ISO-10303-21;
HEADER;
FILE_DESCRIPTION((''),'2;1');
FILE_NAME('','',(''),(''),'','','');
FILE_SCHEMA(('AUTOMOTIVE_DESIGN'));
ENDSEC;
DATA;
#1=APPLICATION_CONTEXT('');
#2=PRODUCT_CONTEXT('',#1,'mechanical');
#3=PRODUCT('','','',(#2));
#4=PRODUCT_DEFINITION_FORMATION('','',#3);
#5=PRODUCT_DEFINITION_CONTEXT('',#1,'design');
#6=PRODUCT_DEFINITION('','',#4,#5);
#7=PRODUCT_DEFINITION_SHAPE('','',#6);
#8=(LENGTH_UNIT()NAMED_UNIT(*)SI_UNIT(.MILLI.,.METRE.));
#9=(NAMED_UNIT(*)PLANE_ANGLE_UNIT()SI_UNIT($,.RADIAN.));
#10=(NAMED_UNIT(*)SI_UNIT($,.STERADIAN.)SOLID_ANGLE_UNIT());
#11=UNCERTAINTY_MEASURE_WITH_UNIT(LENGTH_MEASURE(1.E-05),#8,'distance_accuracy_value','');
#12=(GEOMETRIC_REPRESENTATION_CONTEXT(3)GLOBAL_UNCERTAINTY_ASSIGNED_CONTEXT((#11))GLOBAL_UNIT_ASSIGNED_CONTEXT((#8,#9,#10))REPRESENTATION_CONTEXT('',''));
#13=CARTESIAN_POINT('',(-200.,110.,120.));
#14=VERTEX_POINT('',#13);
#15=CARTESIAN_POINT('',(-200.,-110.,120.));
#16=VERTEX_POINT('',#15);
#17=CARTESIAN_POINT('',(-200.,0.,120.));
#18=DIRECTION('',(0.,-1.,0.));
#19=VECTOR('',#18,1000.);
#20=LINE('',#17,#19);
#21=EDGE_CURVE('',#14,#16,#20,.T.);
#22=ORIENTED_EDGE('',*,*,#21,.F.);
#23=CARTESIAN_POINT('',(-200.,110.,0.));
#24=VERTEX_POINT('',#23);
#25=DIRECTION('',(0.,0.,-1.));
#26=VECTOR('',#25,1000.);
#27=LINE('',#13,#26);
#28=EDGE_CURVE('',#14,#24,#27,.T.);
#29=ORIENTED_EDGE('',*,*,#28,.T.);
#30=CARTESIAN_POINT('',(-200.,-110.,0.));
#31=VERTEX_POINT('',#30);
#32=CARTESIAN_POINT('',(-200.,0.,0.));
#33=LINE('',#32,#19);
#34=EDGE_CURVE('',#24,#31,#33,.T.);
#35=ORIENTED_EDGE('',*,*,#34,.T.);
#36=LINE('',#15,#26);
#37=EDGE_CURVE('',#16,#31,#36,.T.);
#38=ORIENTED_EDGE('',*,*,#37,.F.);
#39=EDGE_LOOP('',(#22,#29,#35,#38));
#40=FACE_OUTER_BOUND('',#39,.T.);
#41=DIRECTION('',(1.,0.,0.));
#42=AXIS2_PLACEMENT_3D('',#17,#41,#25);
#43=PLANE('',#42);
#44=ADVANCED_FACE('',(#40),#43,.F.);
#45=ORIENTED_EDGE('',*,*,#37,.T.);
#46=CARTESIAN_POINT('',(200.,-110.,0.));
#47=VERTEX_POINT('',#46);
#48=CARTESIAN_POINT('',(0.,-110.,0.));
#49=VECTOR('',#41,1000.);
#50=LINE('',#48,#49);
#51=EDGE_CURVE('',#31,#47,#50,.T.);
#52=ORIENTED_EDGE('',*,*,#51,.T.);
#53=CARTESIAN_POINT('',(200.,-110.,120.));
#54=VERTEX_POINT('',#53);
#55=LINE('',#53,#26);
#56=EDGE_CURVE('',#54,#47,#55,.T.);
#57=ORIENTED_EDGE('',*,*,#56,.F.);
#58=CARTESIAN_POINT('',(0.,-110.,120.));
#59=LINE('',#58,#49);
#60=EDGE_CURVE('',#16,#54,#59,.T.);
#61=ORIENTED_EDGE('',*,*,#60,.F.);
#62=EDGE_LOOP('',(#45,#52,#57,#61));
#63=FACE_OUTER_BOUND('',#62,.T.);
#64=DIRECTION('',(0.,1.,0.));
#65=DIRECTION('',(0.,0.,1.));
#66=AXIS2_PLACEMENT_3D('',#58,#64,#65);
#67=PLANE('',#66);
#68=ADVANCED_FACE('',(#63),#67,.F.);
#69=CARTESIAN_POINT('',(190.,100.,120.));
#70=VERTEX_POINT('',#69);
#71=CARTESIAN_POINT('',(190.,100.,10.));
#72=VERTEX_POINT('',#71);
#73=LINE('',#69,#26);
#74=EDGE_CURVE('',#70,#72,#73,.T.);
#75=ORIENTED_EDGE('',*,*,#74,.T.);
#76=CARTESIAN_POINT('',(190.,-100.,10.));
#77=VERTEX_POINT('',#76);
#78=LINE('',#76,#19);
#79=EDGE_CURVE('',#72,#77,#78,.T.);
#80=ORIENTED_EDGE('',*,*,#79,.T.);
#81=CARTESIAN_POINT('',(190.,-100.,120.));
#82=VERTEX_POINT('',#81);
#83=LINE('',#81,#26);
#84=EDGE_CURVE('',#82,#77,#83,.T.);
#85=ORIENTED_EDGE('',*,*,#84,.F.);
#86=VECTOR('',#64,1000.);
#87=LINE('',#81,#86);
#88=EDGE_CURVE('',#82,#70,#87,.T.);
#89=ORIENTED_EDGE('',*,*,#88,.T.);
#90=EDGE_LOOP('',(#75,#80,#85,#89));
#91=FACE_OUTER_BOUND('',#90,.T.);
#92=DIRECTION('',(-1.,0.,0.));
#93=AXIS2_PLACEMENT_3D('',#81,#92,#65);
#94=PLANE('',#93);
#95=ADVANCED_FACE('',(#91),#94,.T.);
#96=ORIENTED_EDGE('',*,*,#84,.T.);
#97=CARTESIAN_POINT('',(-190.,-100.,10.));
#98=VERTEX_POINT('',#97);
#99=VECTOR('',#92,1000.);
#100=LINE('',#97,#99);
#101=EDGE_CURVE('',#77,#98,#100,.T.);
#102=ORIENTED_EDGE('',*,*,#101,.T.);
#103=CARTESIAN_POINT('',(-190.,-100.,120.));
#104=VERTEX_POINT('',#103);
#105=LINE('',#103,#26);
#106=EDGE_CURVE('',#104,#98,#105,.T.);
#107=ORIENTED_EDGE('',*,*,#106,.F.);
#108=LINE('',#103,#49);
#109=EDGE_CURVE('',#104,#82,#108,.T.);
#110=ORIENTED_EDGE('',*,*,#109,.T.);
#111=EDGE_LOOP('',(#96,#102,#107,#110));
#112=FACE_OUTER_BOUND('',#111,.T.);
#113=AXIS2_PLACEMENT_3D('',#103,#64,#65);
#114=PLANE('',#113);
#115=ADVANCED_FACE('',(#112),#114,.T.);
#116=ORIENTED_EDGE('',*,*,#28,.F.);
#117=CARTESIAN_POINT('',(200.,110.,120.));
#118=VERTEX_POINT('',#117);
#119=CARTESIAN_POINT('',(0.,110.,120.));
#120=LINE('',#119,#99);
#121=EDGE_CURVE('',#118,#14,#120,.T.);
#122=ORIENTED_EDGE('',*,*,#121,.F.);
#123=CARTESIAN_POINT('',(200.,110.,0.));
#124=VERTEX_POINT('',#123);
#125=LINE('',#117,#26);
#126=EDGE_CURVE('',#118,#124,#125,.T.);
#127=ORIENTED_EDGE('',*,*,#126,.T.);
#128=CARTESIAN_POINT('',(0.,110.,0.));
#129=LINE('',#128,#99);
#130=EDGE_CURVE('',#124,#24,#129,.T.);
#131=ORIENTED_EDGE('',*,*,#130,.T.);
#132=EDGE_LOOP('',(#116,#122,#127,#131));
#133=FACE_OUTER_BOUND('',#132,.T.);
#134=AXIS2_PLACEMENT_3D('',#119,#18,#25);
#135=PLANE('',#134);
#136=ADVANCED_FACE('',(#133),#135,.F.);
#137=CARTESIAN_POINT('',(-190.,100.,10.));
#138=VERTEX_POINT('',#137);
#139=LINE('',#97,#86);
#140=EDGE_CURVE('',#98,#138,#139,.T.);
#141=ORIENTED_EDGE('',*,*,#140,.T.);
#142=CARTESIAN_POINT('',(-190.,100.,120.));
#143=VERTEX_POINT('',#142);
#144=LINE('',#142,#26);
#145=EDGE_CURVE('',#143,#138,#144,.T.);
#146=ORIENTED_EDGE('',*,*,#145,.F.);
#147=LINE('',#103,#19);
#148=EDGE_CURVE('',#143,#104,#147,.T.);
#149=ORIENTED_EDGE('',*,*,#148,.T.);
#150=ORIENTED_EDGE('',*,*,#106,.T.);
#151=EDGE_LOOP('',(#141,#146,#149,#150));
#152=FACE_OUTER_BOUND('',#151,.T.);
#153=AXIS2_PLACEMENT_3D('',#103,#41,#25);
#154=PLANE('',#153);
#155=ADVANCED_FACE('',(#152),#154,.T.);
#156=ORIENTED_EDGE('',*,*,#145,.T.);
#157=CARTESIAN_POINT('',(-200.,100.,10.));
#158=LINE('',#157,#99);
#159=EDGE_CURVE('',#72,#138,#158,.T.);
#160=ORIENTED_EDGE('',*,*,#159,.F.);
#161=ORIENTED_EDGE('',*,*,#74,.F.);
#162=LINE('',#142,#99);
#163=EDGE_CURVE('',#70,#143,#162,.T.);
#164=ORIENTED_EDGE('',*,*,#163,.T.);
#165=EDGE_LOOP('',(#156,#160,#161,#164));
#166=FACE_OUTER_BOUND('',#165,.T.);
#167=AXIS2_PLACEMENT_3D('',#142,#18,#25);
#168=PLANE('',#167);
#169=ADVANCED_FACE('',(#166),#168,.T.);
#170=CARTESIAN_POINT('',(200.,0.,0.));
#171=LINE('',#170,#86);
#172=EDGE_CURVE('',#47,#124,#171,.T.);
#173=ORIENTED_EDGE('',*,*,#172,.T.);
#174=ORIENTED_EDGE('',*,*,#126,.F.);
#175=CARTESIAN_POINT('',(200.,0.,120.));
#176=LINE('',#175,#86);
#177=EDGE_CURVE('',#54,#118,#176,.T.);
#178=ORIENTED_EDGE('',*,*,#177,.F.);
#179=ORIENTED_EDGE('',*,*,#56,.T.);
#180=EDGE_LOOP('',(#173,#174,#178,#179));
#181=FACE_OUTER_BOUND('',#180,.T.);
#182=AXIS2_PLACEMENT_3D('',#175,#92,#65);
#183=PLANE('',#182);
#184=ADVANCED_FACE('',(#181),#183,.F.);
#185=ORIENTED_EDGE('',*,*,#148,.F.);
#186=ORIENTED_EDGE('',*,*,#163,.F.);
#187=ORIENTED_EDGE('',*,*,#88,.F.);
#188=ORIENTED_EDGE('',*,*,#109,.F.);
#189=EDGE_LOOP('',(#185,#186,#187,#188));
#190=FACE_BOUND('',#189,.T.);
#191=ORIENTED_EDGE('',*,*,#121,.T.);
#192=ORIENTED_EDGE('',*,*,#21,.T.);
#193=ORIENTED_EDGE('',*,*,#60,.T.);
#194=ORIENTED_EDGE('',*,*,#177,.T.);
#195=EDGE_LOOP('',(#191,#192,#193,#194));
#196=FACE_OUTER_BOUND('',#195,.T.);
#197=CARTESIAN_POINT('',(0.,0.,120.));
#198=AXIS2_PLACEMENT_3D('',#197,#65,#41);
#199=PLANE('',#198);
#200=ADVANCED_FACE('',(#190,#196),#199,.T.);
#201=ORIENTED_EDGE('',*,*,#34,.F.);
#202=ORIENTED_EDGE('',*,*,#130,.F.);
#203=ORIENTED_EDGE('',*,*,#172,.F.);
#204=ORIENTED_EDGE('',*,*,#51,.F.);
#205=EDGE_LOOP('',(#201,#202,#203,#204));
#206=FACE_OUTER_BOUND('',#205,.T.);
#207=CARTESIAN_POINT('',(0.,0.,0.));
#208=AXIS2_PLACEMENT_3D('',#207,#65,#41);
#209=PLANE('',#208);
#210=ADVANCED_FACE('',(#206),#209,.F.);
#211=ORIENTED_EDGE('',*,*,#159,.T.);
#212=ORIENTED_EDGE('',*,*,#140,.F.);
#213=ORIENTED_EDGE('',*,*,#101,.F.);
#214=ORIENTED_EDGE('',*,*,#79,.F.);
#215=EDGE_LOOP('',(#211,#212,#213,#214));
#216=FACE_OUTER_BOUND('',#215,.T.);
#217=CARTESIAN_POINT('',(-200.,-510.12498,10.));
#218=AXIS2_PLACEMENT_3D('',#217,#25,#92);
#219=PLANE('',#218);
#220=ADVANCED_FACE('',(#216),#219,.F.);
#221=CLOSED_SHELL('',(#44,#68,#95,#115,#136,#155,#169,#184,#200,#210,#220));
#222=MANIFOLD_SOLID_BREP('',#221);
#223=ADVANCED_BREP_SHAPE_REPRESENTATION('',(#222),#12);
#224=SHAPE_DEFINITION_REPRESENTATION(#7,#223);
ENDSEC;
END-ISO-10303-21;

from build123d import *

# Parameters (mm, degrees)
SKETCH_1_W      = 400
SKETCH_1_H      = 220
SKETCH_1_W_2    = 380
SKETCH_1_H_2    = 200
EXTRUDE_1_DEPTH = 120
SKETCH_2_W      = 400
SKETCH_2_H      = 10
EXTRUDE_2_DEPTH = 210


with BuildPart() as part:
    # 草图1 → 拉伸-薄壁1 (new body)
    with BuildSketch(Plane.XY):
        Rectangle(SKETCH_1_W, SKETCH_1_H)
        Rectangle(SKETCH_1_W_2, SKETCH_1_H_2, mode=Mode.SUBTRACT)
    extrude(amount=EXTRUDE_1_DEPTH)

    # 草图2 → 凸台-拉伸2 (add)
    with BuildSketch(Plane(origin=(0, 100, 0), x_dir=(-1, 0, 0), z_dir=(0, -1, 0))):
        with Locations((0, -5)):
            Rectangle(SKETCH_2_W, SKETCH_2_H)
    extrude(amount=EXTRUDE_2_DEPTH)


solid = part.part
